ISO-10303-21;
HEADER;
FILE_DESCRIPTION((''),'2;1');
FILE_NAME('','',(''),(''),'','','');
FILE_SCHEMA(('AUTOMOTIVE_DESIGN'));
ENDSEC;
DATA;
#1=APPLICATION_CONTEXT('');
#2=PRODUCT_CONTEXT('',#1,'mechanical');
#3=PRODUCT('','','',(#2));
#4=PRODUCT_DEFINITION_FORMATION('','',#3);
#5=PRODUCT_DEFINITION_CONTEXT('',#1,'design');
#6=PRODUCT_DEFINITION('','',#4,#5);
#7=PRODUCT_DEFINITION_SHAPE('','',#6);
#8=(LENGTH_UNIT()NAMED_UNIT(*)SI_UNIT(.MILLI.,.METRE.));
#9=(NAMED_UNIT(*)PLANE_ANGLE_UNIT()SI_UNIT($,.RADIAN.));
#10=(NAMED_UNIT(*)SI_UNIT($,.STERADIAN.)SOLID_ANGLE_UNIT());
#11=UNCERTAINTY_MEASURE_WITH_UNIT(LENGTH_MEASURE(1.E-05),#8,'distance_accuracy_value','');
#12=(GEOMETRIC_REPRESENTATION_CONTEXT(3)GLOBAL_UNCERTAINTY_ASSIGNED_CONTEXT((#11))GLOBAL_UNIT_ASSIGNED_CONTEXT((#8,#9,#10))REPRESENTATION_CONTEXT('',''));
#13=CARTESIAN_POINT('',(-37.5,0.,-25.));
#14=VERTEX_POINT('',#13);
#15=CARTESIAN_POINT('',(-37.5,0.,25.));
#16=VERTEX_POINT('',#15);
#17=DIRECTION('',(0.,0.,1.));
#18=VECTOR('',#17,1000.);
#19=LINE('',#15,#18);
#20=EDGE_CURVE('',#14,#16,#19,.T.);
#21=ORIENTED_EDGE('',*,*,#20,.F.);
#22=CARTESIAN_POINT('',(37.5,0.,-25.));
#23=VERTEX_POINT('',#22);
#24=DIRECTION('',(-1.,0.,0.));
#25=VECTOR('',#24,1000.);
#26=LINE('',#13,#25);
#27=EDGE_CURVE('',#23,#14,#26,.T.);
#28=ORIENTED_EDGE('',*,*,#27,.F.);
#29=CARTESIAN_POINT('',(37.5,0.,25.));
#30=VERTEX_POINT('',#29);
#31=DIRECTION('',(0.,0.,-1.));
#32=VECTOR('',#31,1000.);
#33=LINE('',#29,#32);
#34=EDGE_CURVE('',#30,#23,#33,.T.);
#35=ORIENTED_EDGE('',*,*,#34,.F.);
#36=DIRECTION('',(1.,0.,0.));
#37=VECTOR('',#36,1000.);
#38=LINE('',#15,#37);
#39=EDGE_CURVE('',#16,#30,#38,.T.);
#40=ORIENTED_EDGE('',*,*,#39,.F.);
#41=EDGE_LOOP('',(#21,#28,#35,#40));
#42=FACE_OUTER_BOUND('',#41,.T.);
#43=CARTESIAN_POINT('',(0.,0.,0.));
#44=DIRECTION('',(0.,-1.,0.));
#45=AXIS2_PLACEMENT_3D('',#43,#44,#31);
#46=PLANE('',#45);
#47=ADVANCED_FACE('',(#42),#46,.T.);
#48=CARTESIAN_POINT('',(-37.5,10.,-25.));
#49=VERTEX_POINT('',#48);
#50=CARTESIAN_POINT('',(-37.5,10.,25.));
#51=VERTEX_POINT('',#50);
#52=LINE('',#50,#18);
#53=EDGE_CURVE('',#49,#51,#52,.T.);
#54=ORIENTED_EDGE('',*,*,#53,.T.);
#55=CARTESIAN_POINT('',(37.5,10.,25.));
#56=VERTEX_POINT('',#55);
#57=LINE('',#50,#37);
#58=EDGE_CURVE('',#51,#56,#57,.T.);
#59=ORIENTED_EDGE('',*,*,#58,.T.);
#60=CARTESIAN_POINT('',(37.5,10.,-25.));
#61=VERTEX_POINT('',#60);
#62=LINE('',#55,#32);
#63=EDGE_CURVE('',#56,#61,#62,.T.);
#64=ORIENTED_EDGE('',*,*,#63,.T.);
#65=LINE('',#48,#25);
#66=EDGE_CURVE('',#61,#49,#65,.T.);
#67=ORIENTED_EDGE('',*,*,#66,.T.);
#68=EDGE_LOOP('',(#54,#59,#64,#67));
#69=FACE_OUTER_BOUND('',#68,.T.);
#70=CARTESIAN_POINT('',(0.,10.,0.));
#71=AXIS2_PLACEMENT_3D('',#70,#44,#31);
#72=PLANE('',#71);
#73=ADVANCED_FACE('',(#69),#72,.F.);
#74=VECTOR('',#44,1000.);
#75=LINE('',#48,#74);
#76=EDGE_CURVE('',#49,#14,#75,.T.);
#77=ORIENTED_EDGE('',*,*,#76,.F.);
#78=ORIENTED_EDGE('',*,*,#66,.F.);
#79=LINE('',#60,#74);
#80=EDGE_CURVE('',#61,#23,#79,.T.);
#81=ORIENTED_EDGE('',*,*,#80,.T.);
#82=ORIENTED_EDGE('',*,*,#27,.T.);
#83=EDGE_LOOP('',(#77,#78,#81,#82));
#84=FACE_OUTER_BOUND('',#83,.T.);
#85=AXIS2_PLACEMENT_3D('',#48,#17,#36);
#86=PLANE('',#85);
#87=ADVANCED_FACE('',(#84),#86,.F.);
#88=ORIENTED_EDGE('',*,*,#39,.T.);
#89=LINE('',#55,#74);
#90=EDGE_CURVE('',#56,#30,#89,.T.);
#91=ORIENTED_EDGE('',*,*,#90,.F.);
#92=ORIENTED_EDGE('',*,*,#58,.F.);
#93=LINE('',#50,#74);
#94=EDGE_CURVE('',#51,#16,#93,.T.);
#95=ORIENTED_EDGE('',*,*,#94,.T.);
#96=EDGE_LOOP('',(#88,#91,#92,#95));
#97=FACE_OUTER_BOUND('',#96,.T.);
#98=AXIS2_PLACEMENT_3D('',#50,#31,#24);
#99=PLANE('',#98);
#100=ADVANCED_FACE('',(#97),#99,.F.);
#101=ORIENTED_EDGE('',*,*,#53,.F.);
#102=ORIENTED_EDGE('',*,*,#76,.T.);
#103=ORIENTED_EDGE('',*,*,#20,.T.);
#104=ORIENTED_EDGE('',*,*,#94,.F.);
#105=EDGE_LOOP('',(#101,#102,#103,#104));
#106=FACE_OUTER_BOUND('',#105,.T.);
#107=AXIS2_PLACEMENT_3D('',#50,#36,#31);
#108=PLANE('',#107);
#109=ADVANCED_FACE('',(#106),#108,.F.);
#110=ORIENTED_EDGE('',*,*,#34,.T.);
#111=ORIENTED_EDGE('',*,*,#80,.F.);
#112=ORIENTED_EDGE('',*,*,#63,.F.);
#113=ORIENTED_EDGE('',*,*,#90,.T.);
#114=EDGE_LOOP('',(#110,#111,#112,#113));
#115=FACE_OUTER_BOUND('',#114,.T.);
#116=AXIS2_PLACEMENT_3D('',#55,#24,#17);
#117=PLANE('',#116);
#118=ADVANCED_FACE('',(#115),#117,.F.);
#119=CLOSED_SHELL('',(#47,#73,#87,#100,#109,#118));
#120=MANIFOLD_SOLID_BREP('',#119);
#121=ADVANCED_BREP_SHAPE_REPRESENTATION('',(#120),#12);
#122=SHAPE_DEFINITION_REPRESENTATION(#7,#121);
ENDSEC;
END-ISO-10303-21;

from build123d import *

# Parameters (mm, degrees)
SKETCH_1_W      = 75
SKETCH_1_H      = 50
EXTRUDE_1_DEPTH = 10


with BuildPart() as part:
    # 草图1 → 凸台-拉伸1 (new body)
    with BuildSketch(Plane(origin=(0, 0, 0), x_dir=(1, 0, 0), z_dir=(0, 1, 0))):
        Rectangle(SKETCH_1_W, SKETCH_1_H)
    extrude(amount=EXTRUDE_1_DEPTH)


solid = part.part
